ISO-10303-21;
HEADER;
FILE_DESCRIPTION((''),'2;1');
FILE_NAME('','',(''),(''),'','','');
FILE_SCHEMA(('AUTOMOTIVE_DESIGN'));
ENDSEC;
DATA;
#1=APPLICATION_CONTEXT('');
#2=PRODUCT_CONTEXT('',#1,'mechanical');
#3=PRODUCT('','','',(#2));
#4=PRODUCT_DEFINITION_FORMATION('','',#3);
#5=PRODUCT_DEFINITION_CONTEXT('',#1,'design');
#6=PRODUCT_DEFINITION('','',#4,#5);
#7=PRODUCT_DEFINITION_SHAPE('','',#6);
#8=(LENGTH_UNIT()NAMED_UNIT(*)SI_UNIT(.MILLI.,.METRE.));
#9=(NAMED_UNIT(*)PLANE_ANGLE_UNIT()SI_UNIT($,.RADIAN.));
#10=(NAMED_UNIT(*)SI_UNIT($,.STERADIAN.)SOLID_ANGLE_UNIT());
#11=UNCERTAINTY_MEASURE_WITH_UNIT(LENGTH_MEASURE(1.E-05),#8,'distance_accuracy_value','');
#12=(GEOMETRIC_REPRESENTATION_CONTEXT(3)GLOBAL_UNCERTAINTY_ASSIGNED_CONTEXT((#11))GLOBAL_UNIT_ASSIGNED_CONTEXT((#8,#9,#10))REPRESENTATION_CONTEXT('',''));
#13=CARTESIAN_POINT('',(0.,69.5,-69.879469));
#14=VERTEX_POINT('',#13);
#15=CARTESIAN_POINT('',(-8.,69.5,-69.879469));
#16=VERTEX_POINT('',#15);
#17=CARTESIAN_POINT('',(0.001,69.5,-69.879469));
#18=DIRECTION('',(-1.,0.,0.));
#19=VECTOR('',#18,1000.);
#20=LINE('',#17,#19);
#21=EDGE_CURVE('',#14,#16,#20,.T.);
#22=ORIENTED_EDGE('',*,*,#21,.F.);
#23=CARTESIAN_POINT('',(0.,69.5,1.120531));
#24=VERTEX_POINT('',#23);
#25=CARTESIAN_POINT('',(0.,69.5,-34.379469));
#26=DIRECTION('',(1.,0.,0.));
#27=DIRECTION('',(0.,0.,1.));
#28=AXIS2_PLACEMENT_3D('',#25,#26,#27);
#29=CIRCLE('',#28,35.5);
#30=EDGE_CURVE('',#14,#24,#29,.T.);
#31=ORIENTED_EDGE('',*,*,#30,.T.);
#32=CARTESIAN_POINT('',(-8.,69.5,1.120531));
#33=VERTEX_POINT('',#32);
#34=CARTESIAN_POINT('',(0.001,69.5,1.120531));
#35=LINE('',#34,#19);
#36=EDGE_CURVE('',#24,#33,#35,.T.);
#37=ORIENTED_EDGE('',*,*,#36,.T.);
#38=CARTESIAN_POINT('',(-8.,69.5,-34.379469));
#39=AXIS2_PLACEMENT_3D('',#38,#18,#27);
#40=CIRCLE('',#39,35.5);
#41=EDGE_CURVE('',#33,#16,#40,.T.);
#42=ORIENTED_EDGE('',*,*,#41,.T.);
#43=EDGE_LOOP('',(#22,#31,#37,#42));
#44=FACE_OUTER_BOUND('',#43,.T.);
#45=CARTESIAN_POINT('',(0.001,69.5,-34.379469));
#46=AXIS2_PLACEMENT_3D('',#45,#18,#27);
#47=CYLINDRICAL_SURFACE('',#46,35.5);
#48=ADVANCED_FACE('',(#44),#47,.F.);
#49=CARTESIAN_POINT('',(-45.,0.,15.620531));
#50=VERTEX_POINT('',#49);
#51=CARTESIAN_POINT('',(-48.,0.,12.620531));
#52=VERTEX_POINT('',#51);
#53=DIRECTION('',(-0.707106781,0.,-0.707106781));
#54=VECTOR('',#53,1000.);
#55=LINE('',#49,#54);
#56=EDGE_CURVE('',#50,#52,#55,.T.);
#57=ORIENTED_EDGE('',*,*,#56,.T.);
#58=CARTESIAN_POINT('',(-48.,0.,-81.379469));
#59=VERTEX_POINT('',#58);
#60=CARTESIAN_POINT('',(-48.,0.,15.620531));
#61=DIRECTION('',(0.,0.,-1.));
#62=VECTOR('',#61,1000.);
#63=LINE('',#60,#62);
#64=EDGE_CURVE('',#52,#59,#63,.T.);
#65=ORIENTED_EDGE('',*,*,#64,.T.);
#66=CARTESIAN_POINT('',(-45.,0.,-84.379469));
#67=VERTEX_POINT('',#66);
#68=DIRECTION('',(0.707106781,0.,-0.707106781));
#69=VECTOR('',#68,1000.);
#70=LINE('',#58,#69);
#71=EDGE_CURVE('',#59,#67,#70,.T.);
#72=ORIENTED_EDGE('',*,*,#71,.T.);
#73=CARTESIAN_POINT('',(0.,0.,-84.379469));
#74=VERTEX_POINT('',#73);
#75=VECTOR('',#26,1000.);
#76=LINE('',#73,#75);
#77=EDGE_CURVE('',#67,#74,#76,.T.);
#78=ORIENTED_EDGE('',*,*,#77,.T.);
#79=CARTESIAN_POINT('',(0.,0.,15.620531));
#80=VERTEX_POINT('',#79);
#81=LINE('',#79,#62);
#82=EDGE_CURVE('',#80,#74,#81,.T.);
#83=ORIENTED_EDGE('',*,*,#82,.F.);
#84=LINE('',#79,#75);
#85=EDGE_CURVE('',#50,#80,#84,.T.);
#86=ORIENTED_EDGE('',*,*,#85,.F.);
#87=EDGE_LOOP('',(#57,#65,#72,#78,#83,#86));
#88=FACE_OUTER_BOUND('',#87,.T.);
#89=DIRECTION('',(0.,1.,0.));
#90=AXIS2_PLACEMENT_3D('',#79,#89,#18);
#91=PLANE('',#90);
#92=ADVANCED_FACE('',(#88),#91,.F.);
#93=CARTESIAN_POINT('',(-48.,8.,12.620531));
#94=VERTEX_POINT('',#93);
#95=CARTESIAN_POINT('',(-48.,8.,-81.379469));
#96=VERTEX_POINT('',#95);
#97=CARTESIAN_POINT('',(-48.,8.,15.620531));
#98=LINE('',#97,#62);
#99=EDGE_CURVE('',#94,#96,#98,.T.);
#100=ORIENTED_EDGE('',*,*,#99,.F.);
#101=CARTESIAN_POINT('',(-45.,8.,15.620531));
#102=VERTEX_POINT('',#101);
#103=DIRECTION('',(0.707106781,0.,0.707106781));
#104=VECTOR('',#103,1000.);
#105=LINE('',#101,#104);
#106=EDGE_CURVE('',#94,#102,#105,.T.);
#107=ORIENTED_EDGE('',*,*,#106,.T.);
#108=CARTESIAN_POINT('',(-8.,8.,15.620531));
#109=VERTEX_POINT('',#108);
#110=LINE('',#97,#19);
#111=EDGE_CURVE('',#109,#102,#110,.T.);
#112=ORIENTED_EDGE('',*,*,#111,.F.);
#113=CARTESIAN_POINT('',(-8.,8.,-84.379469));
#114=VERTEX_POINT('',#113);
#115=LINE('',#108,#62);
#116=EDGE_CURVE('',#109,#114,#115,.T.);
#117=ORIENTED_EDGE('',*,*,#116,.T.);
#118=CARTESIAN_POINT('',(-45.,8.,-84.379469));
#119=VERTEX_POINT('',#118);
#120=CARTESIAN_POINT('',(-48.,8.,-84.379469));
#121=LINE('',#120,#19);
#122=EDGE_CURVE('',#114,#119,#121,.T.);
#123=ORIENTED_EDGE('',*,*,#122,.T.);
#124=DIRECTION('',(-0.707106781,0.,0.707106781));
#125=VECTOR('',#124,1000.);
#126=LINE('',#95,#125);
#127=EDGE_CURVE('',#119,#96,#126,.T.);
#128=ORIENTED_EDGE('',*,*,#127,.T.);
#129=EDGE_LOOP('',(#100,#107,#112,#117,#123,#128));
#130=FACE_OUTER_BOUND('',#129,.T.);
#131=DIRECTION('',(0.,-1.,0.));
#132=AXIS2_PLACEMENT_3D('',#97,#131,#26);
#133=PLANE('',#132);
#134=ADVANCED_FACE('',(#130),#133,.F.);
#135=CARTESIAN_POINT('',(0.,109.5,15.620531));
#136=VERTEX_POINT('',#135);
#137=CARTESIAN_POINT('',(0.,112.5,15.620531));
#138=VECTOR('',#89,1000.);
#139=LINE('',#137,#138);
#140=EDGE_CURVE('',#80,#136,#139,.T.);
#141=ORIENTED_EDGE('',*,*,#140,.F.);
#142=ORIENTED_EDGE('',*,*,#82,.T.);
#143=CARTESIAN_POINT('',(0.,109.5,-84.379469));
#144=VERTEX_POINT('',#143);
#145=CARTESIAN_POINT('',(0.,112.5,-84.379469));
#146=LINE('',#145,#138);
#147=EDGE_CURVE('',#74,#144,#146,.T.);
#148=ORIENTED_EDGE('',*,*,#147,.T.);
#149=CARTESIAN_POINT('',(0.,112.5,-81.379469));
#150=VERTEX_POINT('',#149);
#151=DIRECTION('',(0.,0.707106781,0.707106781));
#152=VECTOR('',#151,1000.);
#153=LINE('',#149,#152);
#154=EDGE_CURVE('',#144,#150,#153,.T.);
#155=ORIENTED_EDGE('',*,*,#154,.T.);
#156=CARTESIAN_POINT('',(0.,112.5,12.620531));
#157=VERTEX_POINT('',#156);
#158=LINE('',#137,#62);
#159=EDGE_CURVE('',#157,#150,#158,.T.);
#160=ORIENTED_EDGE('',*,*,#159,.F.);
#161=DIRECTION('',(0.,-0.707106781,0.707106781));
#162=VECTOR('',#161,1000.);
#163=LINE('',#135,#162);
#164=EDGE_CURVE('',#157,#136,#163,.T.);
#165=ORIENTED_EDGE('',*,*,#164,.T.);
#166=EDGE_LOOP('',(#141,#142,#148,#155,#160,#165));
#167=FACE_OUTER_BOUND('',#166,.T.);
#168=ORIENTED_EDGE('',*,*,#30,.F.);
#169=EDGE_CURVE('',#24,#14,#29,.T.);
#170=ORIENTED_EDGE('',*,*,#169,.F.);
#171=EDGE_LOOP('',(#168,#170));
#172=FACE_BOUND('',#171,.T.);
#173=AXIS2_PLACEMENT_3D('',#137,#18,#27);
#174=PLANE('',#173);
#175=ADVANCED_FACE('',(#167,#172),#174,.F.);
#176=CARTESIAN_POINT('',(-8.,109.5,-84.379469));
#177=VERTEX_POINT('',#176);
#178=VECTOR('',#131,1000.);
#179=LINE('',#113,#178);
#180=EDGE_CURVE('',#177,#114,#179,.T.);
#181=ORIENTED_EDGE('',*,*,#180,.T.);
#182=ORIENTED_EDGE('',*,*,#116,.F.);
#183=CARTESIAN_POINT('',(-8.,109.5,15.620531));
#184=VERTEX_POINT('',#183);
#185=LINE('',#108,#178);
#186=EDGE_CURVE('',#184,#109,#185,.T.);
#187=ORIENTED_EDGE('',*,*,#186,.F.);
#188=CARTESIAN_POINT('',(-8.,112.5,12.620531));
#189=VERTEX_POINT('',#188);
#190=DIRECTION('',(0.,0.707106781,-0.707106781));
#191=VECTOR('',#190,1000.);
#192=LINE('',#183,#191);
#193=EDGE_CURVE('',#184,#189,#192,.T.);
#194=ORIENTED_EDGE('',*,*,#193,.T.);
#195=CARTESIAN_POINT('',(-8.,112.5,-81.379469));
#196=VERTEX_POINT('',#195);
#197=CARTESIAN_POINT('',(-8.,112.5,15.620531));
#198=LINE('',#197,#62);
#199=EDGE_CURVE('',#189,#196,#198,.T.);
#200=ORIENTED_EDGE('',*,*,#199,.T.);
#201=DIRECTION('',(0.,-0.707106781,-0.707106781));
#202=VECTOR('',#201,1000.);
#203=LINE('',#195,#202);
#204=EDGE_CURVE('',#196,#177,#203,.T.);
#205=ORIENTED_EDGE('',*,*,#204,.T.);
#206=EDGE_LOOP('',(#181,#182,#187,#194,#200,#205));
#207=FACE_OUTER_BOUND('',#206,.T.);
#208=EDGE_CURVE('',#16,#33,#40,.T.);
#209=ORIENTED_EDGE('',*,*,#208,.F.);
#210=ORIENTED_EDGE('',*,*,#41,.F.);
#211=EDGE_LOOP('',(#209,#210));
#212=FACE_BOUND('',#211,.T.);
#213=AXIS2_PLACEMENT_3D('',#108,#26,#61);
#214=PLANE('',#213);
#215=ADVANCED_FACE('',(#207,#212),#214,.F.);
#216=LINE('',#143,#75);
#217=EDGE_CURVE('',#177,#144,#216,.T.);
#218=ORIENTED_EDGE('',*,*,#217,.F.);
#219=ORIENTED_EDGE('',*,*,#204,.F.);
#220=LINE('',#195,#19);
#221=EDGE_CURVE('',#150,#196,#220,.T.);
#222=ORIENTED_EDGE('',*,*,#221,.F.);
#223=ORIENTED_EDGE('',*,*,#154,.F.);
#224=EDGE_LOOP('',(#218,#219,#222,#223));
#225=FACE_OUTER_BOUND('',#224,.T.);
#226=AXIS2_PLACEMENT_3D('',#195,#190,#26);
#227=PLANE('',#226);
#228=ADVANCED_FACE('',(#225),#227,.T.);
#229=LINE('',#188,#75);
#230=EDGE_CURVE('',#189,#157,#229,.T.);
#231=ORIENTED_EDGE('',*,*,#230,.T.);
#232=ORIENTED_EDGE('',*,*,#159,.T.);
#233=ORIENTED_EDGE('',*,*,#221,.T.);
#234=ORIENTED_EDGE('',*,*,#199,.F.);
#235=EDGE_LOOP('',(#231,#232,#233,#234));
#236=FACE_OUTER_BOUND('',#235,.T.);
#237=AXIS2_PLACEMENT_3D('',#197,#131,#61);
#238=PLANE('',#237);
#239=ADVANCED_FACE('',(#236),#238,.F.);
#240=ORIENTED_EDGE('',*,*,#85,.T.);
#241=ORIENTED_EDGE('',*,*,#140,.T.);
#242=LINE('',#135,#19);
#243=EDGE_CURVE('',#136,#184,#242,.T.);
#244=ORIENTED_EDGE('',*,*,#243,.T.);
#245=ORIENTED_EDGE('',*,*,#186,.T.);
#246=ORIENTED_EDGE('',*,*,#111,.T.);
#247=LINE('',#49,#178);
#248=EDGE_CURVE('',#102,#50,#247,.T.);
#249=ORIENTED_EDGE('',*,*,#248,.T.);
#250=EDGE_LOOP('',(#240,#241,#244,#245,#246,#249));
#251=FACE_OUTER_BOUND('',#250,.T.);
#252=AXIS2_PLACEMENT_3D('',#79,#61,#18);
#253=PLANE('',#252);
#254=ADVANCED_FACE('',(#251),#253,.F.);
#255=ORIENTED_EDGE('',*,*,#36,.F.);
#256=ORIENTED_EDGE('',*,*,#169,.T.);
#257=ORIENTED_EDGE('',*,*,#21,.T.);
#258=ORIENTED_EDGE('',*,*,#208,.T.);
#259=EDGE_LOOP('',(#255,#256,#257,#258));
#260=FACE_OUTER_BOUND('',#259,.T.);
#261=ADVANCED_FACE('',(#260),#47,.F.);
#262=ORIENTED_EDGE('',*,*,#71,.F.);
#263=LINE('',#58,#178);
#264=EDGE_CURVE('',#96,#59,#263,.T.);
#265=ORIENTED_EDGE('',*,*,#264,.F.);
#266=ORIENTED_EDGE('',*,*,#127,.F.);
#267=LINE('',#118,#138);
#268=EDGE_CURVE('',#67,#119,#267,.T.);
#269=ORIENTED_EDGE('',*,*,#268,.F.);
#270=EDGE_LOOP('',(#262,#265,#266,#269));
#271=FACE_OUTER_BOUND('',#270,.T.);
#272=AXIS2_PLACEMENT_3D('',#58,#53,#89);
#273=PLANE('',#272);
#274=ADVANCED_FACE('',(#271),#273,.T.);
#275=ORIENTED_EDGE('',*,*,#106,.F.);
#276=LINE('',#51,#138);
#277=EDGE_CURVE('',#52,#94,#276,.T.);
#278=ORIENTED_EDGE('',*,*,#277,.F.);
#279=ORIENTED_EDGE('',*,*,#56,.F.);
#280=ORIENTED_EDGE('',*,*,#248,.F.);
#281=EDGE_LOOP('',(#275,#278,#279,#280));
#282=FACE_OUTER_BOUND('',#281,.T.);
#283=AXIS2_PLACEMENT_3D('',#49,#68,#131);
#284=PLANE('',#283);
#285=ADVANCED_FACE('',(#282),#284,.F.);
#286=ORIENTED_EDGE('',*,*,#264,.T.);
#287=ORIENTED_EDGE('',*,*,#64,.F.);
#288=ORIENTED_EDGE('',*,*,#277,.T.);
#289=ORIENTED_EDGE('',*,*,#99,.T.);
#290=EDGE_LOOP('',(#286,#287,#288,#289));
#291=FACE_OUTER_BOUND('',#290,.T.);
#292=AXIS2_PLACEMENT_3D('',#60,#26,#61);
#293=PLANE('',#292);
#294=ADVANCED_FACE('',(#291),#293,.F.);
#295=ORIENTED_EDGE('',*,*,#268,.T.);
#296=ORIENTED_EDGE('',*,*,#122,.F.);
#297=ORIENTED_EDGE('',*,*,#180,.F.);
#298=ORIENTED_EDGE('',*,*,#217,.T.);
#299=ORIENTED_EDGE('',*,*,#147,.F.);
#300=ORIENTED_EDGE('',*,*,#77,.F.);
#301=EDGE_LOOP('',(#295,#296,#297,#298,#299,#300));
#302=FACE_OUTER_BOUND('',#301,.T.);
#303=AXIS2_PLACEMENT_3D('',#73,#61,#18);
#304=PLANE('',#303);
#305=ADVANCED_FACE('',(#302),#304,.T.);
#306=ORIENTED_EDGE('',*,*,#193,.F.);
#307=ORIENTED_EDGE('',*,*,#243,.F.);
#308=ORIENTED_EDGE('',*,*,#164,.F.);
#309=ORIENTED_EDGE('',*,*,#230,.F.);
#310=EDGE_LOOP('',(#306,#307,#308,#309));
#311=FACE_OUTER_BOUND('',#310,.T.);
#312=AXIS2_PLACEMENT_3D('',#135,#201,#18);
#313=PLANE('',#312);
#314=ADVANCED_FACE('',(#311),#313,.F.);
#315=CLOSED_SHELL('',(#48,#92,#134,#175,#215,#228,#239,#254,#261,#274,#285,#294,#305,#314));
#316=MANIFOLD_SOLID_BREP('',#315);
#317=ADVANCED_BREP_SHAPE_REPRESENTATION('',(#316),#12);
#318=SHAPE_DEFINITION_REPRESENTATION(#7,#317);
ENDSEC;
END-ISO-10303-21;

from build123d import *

# Parameters (mm, degrees)
EXTRUDE_1_DEPTH     = 50
CHAMFER_1_SIZE      = 3
CUT_EXTRUDE_1_REACH = 148.206
SKETCH_4_R          = 35.5


with BuildPart() as part:
    # 草图2 → 凸台-拉伸1 (new, symmetric)
    with BuildSketch(Plane(origin=(409.637600706, 0.5, -34.379468655), x_dir=(1, 0, 0), z_dir=(0, 0, 1))):
        Polygon((-409.637600706, 112), (-409.637600706, -0.5), (-457.637600706, -0.5), (-457.637600706, 7.5), (-417.637600706, 7.5), (-417.637600706, 112), align=None)
    extrude(amount=EXTRUDE_1_DEPTH, both=True)

    # 倒角1
    chamfer_1_edges = [part.edges().sort_by_distance(p)[0] for p in [
        (-48, 4, 15.620531345),
        (-4, 112.5, 15.620531345),
        (-48, 4, -84.379468655),
        (-4, 112.5, -84.379468655),
    ]]
    chamfer(chamfer_1_edges, length=CHAMFER_1_SIZE)

    # 草图4 → 切除-拉伸1 (cut, up to next)
    with BuildSketch(Plane.ZY.offset(8), mode=Mode.PRIVATE) as cut_extrude_1_sk1:
        with Locations((-34.379468655, 69.5)):
            Circle(SKETCH_4_R)
    cut_extrude_1_tool1 = extrude(cut_extrude_1_sk1.sketch, amount=-CUT_EXTRUDE_1_REACH, mode=Mode.PRIVATE) & part.part
    add(cut_extrude_1_tool1.solids().sort_by_distance((-8, 69.5, -34.379469))[0], mode=Mode.SUBTRACT)


solid = part.part
